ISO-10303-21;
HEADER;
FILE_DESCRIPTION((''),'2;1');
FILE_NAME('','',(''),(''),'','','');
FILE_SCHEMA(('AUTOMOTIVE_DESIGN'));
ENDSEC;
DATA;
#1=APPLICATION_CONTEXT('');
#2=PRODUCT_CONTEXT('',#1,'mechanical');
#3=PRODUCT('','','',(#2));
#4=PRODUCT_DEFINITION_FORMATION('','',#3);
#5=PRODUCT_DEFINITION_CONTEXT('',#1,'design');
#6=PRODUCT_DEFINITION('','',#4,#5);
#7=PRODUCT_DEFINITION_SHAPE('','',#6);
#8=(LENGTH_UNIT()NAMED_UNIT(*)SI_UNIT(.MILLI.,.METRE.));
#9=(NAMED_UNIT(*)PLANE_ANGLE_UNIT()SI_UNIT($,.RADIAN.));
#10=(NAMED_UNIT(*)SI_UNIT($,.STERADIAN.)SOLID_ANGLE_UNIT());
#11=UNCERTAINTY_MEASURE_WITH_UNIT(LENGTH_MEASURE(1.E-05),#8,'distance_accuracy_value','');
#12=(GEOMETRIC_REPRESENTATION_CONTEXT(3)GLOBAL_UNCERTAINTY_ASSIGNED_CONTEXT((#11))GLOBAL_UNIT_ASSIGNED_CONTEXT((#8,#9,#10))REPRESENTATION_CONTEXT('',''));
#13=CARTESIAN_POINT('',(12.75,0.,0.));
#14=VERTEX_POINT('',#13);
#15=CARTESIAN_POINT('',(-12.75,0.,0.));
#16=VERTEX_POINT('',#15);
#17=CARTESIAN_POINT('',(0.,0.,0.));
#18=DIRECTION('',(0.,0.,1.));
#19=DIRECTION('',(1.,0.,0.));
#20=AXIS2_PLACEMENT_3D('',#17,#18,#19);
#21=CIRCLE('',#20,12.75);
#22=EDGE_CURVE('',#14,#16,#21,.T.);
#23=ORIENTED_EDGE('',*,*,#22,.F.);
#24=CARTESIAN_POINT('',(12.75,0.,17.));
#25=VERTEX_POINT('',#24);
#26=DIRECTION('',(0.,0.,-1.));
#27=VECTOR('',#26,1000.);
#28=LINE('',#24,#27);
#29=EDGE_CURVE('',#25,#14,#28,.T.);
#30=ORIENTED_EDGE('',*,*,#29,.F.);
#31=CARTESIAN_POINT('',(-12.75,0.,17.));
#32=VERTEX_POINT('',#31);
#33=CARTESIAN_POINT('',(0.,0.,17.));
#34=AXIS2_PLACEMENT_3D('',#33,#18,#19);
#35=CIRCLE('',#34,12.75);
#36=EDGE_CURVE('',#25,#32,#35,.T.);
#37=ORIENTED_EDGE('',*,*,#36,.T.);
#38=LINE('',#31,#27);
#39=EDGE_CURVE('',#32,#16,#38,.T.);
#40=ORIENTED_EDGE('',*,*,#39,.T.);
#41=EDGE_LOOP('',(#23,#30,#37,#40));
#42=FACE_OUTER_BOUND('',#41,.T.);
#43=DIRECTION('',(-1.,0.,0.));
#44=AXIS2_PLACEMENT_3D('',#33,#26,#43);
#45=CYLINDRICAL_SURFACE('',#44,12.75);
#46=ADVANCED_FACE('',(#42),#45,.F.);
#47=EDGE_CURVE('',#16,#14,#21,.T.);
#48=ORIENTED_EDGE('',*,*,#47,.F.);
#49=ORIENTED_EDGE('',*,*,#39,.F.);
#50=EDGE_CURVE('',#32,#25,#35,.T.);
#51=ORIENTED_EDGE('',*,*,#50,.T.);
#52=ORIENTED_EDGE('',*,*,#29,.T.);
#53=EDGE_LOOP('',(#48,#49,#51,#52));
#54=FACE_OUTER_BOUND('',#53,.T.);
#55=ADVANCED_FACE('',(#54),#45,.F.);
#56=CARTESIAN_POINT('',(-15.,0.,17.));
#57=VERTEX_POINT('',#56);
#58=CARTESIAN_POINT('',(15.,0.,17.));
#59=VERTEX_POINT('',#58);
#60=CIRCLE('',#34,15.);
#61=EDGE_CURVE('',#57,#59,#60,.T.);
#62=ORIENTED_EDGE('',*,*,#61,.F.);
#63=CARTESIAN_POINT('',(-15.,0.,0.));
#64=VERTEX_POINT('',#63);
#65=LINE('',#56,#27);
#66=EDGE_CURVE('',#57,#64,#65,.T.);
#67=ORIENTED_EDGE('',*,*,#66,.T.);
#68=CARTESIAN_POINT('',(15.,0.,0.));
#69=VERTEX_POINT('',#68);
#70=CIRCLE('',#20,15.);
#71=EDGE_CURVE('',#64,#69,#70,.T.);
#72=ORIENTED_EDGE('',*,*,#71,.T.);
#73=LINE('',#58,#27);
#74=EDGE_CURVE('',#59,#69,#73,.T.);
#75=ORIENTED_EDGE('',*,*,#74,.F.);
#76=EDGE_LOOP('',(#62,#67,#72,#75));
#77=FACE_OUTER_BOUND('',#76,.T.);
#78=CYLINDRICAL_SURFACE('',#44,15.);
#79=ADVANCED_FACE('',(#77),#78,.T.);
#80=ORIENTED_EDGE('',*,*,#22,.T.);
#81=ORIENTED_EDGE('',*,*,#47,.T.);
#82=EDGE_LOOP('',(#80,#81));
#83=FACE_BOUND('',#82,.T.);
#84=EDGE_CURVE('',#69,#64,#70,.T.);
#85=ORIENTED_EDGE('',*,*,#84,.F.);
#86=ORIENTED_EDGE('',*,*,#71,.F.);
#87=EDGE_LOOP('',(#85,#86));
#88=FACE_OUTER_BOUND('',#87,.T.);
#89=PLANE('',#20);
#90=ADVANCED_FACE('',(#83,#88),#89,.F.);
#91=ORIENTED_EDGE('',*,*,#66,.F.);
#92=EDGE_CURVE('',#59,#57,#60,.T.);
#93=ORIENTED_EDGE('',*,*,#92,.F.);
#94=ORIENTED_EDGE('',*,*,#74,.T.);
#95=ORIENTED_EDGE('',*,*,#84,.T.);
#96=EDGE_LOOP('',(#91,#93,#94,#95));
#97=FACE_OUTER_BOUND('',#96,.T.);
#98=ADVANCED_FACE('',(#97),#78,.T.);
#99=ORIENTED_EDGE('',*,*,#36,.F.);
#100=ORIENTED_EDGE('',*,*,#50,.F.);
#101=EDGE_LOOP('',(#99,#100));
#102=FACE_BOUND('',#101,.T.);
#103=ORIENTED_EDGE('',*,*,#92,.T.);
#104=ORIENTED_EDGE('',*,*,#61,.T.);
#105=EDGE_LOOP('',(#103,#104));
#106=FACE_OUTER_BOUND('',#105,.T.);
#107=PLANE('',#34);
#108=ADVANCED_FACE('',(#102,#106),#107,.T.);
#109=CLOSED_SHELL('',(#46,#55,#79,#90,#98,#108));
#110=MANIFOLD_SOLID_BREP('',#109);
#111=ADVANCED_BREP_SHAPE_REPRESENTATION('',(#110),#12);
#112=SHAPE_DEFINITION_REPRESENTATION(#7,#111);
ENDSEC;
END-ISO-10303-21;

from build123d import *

# Parameters (mm, degrees)
SKETCH_1_R      = 15
SKETCH_1_R_2    = 12.75
EXTRUDE_1_DEPTH = 17


with BuildPart() as part:
    # 草图1 → 凸台-拉伸1 (new body)
    with BuildSketch(Plane.XY):
        Circle(SKETCH_1_R)
        Circle(SKETCH_1_R_2, mode=Mode.SUBTRACT)
    extrude(amount=EXTRUDE_1_DEPTH)


solid = part.part
